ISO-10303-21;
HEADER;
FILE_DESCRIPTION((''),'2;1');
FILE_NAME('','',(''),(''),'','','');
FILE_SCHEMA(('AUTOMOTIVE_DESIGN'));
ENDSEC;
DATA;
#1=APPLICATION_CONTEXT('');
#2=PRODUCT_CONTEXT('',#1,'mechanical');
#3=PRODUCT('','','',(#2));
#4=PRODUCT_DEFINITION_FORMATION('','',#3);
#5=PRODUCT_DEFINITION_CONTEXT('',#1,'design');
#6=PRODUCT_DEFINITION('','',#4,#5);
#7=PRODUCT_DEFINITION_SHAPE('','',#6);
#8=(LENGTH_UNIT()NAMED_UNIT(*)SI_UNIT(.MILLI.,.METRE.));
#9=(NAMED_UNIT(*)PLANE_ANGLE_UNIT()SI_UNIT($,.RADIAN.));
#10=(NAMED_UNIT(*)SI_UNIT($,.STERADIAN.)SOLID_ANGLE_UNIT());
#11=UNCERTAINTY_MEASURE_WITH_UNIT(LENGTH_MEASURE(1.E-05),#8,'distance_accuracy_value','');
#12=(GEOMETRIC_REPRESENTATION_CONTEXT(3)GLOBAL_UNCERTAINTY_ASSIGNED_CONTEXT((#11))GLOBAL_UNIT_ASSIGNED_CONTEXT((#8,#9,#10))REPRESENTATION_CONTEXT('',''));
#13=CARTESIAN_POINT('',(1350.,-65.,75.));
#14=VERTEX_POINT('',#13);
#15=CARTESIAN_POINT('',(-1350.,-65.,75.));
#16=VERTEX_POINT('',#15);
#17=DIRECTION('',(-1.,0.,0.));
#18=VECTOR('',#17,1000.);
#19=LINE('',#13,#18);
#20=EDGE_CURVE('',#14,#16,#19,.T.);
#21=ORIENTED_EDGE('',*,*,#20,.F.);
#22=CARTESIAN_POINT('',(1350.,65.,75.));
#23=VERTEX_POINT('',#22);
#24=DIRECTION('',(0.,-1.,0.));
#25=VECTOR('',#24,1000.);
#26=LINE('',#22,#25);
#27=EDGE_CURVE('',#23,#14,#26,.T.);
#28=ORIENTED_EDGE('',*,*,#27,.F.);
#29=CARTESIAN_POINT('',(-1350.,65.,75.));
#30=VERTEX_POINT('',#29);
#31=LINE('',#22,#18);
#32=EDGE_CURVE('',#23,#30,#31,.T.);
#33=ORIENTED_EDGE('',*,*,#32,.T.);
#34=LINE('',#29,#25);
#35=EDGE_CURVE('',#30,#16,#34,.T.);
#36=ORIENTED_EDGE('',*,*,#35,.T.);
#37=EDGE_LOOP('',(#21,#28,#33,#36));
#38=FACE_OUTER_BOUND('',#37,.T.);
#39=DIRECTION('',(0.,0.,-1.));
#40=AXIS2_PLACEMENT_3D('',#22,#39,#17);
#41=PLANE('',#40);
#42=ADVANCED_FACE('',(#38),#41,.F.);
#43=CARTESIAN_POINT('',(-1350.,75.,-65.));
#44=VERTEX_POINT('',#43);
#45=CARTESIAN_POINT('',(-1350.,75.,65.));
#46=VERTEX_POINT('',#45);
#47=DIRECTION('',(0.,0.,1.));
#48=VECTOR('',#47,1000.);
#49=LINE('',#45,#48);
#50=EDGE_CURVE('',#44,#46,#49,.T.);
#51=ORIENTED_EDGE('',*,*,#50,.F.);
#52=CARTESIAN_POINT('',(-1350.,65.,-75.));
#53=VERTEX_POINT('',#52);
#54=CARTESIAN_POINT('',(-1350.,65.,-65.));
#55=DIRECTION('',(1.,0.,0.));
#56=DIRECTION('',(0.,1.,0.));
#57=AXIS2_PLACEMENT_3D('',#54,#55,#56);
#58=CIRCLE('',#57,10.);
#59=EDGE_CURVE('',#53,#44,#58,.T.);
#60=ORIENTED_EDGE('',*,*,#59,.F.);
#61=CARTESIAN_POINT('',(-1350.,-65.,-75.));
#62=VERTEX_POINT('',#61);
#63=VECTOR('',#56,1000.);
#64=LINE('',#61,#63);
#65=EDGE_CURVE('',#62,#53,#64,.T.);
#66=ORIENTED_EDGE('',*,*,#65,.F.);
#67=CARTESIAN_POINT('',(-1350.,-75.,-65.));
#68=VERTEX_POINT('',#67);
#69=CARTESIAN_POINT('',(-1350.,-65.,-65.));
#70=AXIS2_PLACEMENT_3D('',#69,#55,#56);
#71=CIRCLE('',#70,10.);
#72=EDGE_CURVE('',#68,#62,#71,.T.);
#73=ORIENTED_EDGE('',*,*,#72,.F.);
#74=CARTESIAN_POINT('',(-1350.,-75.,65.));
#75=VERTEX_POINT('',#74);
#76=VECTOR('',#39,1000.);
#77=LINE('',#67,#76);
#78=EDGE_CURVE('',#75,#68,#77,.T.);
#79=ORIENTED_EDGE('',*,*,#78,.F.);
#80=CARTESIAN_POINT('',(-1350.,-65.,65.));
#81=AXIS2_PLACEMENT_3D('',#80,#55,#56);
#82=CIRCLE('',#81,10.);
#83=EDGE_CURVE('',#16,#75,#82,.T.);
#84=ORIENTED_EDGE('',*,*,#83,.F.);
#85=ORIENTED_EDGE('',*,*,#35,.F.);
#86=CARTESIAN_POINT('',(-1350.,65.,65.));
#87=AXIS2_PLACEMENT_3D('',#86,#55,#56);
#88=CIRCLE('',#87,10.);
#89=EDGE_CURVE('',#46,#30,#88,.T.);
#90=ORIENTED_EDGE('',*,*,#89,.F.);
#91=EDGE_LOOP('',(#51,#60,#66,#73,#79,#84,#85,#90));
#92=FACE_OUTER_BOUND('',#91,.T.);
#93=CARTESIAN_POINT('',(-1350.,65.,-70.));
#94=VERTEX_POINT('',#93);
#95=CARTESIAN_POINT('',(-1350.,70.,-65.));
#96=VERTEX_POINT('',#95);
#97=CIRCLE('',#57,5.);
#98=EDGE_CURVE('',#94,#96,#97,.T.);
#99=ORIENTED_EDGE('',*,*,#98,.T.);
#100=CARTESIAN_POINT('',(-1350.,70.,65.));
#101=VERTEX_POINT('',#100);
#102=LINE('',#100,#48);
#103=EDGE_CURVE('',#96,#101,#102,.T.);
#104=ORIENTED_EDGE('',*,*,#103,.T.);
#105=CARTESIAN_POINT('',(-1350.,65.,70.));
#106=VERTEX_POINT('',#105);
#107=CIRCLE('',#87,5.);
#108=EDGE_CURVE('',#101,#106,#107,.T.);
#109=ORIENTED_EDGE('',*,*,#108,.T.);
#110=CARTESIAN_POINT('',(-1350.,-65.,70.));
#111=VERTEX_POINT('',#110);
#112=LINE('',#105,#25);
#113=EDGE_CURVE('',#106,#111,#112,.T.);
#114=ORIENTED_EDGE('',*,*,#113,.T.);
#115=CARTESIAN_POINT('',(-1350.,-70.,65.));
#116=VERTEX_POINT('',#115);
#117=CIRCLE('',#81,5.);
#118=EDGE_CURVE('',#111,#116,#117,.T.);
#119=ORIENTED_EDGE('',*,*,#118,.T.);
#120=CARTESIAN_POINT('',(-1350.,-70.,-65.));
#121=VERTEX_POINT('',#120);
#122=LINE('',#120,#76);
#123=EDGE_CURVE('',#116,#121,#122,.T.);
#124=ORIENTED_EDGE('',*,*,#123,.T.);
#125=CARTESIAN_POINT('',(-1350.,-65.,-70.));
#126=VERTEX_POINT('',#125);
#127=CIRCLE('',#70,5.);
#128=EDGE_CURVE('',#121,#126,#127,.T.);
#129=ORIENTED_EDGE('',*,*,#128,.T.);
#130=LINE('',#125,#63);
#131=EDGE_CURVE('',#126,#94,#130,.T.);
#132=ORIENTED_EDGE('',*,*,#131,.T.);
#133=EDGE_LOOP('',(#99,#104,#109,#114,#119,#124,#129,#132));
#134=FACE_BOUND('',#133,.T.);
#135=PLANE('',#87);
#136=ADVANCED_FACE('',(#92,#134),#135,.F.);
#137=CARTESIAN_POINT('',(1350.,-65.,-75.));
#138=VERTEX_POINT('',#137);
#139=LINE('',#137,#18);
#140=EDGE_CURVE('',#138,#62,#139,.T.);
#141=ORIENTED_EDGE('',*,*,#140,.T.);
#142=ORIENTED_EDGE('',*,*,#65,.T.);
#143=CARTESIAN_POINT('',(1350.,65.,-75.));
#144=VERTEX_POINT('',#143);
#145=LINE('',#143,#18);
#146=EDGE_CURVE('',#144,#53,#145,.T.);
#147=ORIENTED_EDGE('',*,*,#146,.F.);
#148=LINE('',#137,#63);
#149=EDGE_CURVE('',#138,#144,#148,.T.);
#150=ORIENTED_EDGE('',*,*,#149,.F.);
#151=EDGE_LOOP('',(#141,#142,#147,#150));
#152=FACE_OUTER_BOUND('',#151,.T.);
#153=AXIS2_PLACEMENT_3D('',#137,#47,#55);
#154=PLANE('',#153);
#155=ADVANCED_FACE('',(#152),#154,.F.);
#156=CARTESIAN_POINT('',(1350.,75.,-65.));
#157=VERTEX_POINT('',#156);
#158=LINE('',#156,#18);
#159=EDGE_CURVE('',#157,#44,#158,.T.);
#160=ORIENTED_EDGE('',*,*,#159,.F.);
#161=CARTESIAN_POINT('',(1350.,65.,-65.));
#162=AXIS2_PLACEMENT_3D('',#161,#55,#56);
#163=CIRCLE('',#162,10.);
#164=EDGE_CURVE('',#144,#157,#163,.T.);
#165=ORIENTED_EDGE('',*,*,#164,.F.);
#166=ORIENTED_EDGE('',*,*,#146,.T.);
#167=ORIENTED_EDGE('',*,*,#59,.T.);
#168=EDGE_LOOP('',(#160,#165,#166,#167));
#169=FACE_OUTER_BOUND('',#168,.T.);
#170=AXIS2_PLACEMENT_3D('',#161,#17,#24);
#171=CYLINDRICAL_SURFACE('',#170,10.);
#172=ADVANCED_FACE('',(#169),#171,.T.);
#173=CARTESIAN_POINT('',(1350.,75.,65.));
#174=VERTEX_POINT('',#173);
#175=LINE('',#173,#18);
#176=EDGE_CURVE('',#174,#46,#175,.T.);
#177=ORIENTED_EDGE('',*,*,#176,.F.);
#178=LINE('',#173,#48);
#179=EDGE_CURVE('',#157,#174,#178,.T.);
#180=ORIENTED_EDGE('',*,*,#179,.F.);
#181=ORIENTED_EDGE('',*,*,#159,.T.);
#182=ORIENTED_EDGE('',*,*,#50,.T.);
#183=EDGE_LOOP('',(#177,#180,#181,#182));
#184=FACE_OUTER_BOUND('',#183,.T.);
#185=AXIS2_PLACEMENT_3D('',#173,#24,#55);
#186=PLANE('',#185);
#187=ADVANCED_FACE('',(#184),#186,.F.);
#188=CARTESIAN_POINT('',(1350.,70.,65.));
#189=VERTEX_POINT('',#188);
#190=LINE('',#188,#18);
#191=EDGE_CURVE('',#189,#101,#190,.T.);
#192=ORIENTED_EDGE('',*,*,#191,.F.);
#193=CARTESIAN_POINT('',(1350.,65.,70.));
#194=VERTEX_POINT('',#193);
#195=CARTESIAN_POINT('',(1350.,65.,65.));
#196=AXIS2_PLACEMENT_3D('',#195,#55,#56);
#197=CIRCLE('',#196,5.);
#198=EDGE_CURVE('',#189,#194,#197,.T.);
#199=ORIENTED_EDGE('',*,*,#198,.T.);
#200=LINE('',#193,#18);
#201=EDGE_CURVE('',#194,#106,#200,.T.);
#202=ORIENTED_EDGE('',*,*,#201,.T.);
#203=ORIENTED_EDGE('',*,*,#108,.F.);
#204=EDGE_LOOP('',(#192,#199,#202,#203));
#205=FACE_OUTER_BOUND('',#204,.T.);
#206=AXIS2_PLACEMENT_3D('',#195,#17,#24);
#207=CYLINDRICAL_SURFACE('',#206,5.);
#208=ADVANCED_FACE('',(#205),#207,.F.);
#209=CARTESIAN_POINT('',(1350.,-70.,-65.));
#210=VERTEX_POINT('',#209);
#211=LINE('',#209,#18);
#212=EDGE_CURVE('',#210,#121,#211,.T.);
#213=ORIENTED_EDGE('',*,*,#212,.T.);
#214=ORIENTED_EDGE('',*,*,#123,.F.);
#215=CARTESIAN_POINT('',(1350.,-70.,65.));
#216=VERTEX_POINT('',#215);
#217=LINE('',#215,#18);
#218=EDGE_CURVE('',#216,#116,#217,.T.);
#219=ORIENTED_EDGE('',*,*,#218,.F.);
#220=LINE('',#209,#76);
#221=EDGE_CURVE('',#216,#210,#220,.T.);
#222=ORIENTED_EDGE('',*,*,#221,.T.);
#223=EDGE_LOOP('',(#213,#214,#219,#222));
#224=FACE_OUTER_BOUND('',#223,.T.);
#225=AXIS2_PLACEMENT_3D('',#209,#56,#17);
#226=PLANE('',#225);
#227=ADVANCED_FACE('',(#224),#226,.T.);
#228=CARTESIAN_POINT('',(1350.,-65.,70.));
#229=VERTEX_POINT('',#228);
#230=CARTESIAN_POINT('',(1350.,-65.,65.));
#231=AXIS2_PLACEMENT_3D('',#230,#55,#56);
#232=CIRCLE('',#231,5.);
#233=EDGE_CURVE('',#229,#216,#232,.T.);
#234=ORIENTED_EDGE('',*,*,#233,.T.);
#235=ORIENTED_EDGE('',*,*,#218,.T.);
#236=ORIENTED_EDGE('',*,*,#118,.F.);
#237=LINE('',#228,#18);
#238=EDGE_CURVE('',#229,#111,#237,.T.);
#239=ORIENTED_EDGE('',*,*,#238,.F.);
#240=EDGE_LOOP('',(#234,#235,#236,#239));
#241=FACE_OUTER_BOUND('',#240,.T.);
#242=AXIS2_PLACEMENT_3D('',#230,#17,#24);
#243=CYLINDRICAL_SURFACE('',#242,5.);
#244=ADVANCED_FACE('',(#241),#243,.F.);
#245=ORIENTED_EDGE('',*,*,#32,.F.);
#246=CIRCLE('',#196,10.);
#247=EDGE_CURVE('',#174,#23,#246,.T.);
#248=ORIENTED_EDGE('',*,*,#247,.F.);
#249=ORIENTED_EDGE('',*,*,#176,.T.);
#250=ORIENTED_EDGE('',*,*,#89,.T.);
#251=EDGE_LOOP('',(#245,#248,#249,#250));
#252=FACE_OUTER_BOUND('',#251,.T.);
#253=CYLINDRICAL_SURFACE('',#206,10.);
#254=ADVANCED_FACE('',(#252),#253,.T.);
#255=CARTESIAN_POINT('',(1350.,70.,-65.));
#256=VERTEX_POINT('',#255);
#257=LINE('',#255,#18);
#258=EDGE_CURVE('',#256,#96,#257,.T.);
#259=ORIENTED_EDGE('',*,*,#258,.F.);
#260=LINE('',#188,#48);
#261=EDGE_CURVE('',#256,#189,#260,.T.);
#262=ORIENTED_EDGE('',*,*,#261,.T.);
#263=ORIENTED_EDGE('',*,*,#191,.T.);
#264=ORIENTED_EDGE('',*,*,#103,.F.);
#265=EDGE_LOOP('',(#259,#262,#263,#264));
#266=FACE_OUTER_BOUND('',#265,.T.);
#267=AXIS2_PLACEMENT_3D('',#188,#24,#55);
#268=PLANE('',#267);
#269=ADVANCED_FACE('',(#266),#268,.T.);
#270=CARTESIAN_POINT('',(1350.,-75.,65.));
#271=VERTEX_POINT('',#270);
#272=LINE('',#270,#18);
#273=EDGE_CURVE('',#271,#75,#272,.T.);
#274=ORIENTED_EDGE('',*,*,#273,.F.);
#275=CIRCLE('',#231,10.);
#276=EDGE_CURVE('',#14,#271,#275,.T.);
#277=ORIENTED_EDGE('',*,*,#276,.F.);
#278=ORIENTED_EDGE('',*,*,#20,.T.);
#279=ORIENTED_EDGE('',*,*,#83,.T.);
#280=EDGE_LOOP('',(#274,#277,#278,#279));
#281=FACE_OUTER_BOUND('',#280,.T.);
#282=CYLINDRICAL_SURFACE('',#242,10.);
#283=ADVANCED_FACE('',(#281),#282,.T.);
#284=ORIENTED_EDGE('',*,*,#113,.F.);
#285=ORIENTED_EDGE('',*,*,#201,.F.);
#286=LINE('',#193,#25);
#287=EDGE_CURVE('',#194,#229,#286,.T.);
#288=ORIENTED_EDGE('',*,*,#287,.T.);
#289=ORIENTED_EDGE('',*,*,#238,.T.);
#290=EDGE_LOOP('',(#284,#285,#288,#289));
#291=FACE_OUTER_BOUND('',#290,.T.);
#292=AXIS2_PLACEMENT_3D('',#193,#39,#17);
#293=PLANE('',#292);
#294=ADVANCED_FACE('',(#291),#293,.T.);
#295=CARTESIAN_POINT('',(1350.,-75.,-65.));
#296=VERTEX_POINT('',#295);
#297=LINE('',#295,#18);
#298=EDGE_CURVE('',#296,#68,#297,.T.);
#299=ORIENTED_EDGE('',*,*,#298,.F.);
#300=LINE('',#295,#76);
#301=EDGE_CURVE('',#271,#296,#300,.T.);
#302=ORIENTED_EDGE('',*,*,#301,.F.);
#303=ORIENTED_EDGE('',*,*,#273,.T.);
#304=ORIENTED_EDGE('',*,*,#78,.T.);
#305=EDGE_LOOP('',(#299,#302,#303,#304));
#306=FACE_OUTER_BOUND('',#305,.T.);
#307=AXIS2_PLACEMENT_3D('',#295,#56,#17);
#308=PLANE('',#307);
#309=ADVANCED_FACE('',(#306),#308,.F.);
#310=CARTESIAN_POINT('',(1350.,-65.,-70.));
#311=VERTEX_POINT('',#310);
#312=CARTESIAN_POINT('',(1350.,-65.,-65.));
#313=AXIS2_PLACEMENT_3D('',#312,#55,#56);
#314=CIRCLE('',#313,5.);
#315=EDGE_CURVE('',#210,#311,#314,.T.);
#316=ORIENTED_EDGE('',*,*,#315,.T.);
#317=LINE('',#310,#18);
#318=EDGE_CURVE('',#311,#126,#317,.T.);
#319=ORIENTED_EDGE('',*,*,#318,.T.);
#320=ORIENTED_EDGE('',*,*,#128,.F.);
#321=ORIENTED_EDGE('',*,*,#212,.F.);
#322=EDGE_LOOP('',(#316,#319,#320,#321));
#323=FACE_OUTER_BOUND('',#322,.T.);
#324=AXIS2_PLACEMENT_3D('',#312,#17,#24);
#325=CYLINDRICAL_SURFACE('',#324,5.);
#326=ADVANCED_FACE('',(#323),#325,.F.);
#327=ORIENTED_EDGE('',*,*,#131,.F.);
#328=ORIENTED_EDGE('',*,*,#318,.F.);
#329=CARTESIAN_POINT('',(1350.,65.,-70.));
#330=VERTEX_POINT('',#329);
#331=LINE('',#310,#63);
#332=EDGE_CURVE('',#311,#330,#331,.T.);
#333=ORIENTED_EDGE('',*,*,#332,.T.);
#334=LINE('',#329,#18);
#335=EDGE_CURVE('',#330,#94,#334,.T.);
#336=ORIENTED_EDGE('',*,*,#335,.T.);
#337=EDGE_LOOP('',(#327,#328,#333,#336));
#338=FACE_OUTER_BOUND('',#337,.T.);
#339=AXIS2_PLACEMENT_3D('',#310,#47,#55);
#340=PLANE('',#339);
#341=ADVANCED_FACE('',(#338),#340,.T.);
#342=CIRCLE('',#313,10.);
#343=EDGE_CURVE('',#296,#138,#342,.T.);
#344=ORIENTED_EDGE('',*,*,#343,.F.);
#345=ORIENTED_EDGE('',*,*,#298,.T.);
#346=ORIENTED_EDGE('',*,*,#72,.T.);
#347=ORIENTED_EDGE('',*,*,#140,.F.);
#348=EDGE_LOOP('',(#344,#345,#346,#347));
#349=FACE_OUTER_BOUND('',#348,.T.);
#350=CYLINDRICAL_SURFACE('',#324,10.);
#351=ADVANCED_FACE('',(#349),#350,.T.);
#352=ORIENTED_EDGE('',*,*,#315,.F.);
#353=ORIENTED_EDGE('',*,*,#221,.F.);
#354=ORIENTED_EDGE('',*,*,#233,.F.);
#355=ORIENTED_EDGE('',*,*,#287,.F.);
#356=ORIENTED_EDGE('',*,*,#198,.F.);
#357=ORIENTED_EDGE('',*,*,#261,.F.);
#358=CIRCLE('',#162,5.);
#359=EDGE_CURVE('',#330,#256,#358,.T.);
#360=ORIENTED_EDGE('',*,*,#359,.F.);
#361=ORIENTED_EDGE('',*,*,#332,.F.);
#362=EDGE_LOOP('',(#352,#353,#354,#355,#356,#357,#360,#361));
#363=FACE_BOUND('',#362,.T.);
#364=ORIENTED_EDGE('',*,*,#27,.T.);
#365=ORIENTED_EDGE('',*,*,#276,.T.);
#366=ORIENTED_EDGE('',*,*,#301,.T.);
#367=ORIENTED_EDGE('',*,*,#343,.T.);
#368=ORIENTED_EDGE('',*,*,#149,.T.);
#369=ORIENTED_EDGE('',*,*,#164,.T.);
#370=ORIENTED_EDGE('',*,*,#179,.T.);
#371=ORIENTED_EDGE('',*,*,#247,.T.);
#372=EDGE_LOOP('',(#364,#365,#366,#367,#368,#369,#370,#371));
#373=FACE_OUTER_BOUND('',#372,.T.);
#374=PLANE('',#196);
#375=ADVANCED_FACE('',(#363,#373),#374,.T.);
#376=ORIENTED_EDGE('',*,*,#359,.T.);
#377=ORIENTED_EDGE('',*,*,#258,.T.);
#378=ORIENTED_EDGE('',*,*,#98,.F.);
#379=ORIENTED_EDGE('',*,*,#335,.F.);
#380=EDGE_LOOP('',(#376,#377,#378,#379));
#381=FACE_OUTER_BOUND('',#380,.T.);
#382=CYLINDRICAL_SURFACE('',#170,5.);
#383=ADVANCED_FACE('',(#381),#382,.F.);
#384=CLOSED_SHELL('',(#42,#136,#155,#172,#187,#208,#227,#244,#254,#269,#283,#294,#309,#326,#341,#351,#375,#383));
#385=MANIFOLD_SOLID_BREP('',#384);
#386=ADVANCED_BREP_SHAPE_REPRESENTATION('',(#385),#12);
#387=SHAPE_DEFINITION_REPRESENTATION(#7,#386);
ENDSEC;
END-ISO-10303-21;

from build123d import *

# Parameters (mm, degrees)
GB_6728_1986_150_X_150_X_5_1_DEPTH = 2700


with BuildPart() as part:
    # Sketch1 → Gb／6728-1986方形空心型钢 150 X 150 X 5(1) (new body)
    with BuildSketch(Plane.YZ.offset(-1350)):
        with BuildLine():
            Line((-65, -75), (65, -75))
            ThreePointArc((65, -75), (72.071067812, -72.071067812), (75, -65))
            Line((75, -65), (75, 65))
            ThreePointArc((75, 65), (72.071067812, 72.071067812), (65, 75))
            Line((65, 75), (-65, 75))
            ThreePointArc((-65, 75), (-72.071067812, 72.071067812), (-75, 65))
            Line((-75, 65), (-75, -65))
            ThreePointArc((-75, -65), (-72.071067812, -72.071067812), (-65, -75))
        make_face()
        with BuildLine():
            Line((-65, -70), (65, -70))
            ThreePointArc((65, -70), (68.535533906, -68.535533906), (70, -65))
            Line((70, -65), (70, 65))
            ThreePointArc((70, 65), (68.535533906, 68.535533906), (65, 70))
            Line((65, 70), (-65, 70))
            ThreePointArc((-65, 70), (-68.535533906, 68.535533906), (-70, 65))
            Line((-70, 65), (-70, -65))
            ThreePointArc((-70, -65), (-68.535533906, -68.535533906), (-65, -70))
        make_face(mode=Mode.SUBTRACT)
    extrude(amount=GB_6728_1986_150_X_150_X_5_1_DEPTH)


solid = part.part
